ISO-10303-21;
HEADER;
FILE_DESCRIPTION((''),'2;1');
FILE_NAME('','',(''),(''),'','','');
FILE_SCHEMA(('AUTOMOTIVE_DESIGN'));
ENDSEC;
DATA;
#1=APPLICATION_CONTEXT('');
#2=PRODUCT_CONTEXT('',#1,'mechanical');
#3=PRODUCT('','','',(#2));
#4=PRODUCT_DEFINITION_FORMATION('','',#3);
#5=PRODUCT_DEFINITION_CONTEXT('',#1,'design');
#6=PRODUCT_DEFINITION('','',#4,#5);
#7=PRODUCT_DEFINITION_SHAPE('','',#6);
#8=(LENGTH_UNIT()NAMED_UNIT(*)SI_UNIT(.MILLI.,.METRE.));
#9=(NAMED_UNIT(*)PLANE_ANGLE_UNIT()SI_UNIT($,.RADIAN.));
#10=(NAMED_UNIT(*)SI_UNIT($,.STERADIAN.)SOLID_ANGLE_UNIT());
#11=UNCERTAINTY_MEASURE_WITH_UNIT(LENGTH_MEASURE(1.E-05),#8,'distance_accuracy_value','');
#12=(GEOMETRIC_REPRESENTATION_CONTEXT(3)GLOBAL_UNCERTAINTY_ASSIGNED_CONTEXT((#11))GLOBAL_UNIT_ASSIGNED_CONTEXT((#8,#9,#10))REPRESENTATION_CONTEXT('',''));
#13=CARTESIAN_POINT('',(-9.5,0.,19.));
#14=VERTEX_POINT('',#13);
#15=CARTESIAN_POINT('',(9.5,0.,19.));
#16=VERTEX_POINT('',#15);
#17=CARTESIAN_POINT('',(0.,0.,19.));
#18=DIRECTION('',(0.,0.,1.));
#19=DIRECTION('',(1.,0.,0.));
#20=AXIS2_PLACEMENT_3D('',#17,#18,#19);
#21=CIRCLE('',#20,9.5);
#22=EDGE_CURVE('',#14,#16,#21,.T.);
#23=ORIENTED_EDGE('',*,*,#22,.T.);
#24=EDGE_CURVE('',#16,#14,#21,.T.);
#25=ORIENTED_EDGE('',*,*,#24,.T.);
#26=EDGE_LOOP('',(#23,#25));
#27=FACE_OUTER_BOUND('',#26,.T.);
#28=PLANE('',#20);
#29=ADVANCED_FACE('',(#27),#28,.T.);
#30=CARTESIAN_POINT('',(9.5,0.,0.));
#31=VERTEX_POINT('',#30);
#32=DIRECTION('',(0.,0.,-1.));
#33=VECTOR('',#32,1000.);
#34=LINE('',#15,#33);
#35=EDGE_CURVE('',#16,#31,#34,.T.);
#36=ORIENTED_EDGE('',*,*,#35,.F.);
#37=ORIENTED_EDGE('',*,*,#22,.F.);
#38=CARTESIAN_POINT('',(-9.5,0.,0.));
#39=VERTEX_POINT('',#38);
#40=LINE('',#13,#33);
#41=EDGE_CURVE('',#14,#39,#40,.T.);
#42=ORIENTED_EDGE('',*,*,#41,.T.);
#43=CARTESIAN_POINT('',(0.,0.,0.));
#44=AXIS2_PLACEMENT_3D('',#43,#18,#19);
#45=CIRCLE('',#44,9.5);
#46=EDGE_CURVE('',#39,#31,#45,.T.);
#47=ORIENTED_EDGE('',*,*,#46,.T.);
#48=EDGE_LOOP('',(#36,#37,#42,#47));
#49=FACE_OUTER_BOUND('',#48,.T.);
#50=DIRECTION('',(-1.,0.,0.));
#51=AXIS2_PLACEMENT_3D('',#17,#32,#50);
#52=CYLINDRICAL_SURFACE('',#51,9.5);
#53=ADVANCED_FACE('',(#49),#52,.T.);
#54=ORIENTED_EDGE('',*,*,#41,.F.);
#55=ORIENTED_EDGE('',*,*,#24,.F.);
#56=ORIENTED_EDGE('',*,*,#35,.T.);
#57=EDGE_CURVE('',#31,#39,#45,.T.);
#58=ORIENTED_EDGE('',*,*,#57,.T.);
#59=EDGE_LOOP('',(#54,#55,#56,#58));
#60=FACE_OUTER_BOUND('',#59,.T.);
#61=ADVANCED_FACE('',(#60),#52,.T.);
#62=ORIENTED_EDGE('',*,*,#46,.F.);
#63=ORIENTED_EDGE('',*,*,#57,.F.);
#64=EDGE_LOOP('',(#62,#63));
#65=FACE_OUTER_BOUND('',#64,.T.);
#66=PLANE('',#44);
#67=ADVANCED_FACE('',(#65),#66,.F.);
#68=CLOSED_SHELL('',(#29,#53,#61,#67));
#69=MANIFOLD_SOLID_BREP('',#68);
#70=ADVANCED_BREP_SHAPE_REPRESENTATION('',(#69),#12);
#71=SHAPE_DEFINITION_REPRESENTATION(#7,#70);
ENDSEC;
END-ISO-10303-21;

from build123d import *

# Parameters (mm, degrees)
SKETCH1_R           = 9.5
BOSS_EXTRUDE1_DEPTH = 19


with BuildPart() as part:
    # Sketch1 → Boss-Extrude1 (new body)
    with BuildSketch(Plane.XY):
        Circle(SKETCH1_R)
    extrude(amount=BOSS_EXTRUDE1_DEPTH)


solid = part.part
